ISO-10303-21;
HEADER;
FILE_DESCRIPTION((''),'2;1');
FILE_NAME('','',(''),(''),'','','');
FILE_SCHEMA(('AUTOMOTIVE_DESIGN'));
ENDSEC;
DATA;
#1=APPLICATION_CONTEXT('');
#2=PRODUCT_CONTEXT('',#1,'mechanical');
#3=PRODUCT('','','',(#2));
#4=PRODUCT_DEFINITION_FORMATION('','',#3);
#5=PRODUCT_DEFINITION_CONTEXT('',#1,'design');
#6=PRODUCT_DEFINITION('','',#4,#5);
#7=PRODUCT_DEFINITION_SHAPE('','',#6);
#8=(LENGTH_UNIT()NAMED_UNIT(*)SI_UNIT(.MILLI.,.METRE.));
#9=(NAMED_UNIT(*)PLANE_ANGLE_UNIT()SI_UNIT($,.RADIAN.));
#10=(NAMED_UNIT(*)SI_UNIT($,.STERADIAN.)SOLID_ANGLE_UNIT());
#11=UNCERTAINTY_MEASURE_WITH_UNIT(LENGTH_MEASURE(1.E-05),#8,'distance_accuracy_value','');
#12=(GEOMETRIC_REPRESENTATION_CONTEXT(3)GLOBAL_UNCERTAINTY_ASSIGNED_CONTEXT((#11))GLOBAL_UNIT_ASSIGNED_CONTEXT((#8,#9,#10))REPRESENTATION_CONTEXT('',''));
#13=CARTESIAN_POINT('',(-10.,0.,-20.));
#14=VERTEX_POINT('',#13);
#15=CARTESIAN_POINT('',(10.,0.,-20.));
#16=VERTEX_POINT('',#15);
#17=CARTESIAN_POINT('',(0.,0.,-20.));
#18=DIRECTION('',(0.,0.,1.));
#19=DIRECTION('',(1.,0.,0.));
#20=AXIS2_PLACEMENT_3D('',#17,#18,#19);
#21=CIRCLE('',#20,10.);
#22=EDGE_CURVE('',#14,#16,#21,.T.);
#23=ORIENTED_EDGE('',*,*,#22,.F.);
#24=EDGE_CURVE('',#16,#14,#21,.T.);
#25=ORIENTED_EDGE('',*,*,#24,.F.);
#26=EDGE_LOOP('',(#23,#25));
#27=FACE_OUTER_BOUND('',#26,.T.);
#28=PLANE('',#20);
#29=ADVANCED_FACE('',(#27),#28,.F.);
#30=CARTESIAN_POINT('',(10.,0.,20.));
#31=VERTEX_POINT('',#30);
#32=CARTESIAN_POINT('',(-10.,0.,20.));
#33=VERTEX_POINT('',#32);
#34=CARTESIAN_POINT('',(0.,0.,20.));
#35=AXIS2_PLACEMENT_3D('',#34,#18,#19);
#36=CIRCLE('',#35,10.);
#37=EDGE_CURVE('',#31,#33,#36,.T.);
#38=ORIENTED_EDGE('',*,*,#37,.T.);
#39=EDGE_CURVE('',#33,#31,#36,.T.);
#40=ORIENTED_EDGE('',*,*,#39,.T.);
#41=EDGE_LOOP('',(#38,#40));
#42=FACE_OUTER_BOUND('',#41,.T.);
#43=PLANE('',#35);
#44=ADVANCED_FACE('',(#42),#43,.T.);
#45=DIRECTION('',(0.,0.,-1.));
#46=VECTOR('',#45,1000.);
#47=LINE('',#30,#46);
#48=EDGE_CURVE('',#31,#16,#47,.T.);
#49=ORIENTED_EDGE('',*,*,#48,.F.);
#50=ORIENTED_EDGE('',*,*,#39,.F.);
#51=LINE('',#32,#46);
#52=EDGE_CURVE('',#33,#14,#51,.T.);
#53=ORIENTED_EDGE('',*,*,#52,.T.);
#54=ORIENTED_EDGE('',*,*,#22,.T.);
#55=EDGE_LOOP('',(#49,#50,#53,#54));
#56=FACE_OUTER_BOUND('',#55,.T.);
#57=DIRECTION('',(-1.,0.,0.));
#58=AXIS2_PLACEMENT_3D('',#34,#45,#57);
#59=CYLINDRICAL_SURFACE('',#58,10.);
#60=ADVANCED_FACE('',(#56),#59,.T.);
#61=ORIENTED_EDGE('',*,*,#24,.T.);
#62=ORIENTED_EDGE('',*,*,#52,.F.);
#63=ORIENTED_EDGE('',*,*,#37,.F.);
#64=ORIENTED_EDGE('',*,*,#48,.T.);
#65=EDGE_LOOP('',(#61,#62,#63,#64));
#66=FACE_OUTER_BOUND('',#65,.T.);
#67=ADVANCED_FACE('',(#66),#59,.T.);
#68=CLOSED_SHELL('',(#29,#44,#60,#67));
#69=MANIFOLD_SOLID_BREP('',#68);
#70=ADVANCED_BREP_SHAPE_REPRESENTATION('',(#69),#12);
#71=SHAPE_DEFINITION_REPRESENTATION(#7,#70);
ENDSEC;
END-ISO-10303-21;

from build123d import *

# Parameters (mm, degrees)
SKETCH1_R           = 10
BOSS_EXTRUDE1_DEPTH = 20


with BuildPart() as part:
    # Sketch1 → Boss-Extrude1 (new, symmetric)
    with BuildSketch(Plane.XY):
        Circle(SKETCH1_R)
    extrude(amount=BOSS_EXTRUDE1_DEPTH, both=True)


solid = part.part
